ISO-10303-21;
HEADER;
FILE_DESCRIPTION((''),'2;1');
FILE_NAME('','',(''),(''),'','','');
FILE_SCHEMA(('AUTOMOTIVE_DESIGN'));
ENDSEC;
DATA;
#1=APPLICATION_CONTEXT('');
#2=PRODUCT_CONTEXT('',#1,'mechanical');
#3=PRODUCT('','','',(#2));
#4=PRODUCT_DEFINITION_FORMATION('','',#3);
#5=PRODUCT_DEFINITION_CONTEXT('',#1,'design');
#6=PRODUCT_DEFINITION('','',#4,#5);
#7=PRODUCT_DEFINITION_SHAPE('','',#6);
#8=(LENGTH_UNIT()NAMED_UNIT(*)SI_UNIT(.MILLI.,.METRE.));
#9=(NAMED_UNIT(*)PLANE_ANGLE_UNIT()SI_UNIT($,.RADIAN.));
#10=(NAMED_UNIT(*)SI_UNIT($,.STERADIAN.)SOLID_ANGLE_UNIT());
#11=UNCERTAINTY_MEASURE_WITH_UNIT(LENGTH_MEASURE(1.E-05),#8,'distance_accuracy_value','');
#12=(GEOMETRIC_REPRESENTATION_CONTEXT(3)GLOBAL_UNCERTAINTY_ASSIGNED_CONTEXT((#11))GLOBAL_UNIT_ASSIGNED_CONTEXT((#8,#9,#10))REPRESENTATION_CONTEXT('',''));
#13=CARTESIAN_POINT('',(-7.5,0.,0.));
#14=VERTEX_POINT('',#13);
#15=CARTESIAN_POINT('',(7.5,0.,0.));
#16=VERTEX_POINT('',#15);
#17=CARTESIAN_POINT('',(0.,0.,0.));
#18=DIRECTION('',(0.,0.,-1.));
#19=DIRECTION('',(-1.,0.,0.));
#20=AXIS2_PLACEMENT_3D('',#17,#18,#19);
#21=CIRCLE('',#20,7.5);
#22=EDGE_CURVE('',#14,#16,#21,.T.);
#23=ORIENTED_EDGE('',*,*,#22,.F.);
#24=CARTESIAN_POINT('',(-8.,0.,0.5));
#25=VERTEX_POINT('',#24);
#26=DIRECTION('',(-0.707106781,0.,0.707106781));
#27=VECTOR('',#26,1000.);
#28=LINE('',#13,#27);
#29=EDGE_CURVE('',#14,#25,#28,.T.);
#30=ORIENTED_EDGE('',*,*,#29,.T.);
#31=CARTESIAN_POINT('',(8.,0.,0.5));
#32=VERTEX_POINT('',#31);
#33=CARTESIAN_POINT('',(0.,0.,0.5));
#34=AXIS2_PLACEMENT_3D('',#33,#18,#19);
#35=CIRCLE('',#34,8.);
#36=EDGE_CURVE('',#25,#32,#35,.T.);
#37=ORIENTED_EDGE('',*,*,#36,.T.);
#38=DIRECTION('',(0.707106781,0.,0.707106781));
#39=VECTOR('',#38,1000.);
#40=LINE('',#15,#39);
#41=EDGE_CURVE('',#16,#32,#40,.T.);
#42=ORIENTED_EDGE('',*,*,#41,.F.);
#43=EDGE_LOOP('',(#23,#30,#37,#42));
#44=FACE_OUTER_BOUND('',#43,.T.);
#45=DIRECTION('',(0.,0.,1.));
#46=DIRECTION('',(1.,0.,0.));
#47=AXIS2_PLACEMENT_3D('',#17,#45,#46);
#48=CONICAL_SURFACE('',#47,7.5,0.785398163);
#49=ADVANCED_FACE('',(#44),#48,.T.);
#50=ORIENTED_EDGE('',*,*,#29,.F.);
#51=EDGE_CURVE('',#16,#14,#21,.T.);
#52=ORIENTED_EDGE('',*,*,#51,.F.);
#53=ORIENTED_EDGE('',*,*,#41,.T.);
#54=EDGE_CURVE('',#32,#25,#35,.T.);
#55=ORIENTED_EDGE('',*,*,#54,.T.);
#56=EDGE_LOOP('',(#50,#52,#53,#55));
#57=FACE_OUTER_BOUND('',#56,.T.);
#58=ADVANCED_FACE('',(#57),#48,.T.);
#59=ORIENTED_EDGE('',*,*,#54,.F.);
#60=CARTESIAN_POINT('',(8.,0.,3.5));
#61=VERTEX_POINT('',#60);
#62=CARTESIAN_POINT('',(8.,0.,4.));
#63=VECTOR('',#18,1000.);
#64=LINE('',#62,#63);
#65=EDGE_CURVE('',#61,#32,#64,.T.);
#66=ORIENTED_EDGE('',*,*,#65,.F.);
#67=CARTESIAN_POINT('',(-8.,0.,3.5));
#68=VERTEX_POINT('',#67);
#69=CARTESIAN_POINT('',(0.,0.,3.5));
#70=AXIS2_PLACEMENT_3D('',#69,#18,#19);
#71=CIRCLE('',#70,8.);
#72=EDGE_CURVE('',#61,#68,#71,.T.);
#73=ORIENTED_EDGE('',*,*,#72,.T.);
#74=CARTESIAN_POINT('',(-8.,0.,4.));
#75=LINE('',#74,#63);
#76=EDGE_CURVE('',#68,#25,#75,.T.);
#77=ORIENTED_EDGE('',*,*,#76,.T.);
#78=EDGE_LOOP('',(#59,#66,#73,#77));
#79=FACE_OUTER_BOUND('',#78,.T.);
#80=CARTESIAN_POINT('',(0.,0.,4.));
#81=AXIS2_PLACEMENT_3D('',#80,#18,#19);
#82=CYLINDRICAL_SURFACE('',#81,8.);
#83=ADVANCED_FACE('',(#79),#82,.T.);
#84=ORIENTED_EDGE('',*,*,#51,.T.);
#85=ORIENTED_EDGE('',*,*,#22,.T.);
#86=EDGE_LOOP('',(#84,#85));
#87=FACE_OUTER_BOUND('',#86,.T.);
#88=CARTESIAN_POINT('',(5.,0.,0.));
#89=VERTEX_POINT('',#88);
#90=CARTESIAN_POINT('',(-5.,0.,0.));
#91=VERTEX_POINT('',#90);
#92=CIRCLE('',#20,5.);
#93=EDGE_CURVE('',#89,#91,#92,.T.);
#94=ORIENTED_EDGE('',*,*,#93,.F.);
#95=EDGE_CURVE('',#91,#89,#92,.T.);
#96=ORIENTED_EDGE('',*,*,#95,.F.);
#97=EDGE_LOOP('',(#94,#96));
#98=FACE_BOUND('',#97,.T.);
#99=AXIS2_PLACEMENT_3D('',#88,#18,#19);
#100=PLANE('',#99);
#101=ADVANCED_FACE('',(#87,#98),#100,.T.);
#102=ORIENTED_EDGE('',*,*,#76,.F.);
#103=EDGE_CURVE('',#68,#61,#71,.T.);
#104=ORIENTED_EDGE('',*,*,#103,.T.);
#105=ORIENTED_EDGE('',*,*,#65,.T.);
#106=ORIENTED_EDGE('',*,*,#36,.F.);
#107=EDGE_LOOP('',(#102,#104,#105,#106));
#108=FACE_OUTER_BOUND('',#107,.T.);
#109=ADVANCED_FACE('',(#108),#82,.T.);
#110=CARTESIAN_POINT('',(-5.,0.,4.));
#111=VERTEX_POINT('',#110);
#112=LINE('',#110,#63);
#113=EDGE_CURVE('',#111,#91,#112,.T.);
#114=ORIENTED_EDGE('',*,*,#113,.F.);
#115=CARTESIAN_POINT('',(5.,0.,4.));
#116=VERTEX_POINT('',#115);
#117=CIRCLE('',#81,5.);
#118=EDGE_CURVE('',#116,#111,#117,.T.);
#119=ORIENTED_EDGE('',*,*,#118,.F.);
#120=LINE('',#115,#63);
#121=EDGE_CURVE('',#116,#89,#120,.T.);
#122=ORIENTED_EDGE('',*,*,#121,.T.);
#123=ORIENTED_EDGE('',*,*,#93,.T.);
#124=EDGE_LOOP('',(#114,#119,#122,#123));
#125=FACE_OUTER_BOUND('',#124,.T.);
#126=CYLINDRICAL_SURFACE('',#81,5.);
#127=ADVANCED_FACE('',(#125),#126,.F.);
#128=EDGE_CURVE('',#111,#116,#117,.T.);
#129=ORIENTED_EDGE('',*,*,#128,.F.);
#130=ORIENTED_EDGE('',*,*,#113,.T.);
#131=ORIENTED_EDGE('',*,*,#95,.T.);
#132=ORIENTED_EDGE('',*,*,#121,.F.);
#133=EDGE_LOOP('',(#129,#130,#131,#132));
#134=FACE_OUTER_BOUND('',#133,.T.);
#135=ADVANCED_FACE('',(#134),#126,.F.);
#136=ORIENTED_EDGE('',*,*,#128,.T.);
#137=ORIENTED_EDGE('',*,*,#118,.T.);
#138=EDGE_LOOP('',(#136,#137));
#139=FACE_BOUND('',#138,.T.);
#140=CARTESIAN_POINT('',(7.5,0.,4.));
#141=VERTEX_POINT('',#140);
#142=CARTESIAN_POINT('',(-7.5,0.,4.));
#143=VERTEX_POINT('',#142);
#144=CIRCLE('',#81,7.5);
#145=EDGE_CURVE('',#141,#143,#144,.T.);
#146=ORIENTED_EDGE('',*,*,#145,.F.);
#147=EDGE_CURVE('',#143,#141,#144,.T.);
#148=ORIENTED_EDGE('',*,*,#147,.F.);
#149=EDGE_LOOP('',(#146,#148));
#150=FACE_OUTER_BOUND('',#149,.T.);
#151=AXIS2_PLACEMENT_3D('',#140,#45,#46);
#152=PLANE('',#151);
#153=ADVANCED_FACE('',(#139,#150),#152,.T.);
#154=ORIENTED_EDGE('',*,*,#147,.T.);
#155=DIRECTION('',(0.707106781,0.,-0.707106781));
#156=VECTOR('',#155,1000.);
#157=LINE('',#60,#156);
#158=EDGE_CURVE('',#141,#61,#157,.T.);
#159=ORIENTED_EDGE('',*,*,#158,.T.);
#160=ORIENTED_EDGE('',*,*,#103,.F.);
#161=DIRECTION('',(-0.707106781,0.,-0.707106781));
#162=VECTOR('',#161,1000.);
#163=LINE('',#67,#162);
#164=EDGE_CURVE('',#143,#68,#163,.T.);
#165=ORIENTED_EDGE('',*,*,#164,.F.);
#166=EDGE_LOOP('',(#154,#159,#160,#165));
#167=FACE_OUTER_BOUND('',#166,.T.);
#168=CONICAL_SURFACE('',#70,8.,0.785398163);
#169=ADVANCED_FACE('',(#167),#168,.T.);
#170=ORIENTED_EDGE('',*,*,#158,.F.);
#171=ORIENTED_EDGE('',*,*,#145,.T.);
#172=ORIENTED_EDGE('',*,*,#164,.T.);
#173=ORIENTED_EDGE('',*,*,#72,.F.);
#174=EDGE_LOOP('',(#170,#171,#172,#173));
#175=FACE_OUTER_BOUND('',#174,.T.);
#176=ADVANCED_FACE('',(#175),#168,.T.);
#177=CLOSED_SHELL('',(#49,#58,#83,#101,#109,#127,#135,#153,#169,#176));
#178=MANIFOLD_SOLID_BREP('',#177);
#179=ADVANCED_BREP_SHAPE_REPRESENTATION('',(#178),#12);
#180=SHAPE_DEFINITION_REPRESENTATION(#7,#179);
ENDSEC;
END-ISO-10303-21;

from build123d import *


with BuildPart() as part:
    # Sketch1 → Revolve1 (revolve)
    with BuildSketch(Plane.XZ, mode=Mode.PRIVATE) as revolve1_sk:
        Polygon((5, 4), (5, 0), (7.5, 0), (8, 0.5), (8, 3.5), (7.5, 4), align=None)
    revolve(revolve1_sk.sketch.rotate(Axis((0, 0, 4), (0, 0, -1)), 180), axis=Axis((0, 0, 4), (0, 0, -1)))


solid = part.part
